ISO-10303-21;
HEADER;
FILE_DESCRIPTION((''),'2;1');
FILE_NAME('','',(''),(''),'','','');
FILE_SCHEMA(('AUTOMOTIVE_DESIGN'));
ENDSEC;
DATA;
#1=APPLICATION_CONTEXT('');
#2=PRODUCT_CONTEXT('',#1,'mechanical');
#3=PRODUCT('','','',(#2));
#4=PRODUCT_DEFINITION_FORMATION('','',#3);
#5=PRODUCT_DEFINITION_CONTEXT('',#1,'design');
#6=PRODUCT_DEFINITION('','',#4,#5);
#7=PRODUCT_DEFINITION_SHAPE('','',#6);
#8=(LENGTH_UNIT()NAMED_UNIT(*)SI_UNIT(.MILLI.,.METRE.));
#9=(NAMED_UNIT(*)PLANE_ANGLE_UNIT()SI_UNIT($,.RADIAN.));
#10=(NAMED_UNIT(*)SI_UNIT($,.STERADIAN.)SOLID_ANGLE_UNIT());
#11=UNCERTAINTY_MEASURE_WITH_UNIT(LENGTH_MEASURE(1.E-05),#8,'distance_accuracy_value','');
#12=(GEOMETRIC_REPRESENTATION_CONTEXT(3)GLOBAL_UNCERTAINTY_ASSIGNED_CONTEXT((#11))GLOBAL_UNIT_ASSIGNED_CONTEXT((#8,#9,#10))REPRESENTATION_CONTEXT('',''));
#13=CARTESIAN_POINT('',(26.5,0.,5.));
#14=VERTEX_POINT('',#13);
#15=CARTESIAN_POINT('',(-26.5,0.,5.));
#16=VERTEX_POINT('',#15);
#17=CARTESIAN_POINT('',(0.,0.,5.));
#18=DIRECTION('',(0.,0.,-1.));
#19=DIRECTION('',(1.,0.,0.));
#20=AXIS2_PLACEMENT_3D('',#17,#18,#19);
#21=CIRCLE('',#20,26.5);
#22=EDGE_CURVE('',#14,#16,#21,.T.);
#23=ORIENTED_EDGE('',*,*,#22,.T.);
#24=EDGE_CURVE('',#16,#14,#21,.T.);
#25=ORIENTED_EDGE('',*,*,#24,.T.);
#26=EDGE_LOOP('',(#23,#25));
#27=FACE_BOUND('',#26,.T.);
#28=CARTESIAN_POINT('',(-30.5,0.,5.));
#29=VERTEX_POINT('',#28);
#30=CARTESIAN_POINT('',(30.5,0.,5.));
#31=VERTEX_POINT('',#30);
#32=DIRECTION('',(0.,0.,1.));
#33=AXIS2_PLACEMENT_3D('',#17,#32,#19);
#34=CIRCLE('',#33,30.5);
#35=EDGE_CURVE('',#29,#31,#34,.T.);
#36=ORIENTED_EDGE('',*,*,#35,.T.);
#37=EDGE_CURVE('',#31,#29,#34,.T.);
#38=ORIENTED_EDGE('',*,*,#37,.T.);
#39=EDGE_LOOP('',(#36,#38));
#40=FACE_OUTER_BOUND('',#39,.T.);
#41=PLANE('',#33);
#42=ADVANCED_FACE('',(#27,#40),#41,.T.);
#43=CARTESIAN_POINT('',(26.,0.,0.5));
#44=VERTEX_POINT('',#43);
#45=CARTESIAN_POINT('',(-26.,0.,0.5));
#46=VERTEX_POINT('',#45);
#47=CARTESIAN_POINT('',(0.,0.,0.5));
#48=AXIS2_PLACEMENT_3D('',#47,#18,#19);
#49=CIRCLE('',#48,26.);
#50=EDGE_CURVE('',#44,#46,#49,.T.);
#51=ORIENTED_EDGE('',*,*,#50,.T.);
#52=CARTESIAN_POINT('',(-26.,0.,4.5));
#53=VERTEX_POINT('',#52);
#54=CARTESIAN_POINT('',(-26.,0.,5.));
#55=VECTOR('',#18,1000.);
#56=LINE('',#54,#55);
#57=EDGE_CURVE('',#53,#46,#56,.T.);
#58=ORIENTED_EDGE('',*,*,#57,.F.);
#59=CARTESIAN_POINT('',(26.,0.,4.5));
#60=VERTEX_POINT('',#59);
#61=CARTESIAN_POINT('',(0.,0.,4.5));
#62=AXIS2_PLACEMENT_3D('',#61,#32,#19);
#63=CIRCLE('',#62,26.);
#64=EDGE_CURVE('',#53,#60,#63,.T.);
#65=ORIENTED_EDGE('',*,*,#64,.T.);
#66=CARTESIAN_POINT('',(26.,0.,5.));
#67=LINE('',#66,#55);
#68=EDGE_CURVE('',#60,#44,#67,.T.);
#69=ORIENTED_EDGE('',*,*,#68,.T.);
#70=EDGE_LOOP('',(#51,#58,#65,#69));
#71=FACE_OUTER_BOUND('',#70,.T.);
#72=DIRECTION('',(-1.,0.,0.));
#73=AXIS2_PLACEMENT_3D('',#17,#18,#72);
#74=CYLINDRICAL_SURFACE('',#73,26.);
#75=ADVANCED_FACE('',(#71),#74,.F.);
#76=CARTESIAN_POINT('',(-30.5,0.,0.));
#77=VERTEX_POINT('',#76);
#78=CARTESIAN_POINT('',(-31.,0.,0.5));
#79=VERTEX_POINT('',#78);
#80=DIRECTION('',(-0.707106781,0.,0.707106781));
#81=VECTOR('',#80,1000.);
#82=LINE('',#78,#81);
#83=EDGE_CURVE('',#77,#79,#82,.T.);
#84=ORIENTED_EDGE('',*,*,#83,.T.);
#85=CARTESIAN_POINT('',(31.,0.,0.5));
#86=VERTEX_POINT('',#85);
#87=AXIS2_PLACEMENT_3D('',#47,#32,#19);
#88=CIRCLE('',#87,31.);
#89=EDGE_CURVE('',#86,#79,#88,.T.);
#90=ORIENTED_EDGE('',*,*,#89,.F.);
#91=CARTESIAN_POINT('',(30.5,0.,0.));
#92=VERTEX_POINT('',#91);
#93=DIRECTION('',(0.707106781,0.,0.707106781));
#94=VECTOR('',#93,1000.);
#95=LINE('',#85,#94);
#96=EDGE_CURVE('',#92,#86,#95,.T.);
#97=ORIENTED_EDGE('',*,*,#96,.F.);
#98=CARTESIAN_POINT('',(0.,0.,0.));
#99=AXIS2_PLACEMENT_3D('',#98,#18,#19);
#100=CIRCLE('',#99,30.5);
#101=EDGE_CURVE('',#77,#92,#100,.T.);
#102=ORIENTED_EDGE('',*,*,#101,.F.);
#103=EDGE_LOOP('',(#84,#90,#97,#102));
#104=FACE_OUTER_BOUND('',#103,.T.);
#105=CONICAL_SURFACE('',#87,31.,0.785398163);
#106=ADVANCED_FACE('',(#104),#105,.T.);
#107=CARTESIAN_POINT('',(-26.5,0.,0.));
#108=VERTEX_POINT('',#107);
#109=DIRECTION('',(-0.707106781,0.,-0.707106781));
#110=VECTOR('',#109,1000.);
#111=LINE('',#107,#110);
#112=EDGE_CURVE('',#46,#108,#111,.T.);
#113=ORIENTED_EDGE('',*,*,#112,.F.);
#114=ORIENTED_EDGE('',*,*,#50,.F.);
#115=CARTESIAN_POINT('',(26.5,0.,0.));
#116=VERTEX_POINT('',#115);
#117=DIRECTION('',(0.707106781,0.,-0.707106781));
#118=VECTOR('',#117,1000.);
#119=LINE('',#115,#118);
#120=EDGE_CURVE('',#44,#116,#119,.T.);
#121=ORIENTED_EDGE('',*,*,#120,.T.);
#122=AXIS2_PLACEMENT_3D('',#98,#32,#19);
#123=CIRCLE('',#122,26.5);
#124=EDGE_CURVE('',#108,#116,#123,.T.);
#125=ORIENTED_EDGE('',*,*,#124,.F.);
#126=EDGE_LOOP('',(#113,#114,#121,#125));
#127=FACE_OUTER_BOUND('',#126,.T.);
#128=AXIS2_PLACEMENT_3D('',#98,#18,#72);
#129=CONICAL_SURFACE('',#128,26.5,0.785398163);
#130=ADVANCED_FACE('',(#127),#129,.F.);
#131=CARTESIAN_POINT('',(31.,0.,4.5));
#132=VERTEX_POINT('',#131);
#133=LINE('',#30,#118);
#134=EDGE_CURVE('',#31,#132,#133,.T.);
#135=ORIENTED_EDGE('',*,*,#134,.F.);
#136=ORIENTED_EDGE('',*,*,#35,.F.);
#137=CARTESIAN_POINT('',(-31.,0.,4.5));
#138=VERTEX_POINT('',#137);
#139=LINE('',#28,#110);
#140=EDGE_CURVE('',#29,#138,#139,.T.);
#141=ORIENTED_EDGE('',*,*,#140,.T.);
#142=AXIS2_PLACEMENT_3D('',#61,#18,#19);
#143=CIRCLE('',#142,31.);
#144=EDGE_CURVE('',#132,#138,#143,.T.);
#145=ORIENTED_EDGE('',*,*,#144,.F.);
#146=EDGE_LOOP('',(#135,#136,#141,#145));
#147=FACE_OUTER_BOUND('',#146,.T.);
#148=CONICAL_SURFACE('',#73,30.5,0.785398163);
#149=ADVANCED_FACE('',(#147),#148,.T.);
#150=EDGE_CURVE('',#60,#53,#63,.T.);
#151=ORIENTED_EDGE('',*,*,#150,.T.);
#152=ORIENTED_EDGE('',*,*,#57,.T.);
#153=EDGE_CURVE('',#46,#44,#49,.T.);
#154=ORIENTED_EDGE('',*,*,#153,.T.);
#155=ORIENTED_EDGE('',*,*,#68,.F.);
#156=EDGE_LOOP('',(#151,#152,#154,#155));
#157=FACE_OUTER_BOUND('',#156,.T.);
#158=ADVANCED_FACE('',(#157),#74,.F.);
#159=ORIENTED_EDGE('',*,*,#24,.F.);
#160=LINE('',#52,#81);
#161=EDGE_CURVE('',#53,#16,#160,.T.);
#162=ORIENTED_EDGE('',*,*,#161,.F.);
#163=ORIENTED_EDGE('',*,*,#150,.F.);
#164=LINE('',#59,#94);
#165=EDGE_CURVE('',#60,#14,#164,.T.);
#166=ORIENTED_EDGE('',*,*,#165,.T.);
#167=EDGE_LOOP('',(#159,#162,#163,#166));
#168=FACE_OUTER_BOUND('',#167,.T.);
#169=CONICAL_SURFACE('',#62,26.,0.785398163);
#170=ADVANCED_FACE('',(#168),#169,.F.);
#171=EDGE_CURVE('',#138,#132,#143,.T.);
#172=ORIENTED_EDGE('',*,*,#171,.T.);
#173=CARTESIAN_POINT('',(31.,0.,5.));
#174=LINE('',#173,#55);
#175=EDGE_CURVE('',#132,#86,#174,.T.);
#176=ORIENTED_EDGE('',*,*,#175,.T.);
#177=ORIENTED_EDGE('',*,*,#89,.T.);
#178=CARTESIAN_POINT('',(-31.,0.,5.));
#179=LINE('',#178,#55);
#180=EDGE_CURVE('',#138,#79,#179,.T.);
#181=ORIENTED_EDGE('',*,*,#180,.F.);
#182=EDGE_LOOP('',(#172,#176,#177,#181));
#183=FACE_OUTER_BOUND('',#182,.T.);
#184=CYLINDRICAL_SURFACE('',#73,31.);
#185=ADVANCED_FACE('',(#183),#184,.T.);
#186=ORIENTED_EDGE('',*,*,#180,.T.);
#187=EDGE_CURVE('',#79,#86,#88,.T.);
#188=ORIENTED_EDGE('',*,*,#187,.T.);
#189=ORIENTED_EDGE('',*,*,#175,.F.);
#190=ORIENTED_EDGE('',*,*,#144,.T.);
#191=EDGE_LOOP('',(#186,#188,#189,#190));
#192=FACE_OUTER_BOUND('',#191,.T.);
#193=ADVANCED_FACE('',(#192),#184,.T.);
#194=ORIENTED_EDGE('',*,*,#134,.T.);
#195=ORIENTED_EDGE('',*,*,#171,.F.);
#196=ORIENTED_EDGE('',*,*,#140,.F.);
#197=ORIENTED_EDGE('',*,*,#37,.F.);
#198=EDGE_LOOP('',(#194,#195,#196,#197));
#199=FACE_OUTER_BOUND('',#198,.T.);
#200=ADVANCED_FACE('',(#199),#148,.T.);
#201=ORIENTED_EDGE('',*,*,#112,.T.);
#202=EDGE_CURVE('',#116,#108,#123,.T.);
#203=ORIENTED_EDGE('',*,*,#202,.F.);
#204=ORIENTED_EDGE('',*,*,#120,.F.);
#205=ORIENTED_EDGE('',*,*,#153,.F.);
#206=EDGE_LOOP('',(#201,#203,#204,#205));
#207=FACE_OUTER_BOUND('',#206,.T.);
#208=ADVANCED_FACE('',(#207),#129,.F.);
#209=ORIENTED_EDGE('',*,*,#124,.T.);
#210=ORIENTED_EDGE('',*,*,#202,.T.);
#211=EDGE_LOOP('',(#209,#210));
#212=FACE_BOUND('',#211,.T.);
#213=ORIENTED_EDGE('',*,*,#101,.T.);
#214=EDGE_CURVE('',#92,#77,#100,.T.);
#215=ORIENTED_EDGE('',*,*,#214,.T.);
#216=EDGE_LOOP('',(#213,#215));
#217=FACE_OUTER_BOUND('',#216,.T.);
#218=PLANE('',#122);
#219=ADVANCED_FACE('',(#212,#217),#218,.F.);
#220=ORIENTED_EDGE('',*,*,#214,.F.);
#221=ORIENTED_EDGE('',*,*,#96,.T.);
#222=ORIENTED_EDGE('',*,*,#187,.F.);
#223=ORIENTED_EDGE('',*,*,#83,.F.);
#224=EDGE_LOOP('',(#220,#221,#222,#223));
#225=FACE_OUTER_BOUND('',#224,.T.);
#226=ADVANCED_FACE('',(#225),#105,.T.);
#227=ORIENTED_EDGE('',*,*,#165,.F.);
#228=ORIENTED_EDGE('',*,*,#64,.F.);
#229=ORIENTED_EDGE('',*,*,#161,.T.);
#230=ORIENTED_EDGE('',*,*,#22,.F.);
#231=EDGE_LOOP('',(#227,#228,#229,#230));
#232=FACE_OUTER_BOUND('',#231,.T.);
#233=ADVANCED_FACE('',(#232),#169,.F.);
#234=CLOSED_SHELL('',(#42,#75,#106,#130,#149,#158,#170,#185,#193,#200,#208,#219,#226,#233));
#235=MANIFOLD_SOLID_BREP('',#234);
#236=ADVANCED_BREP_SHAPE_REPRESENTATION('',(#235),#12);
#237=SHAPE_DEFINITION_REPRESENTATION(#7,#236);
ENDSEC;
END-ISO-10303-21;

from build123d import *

# Parameters (mm, degrees)
SKETCH1_R           = 31
SKETCH1_R_2         = 26
BOSS_EXTRUDE1_DEPTH = 5
CHAMFER1_SIZE       = 0.5


with BuildPart() as part:
    # Sketch1 → Boss-Extrude1 (new body)
    with BuildSketch(Plane.XY):
        Circle(SKETCH1_R)
        Circle(SKETCH1_R_2, mode=Mode.SUBTRACT)
    extrude(amount=BOSS_EXTRUDE1_DEPTH)

    # Chamfer1
    chamfer1_edges = [part.edges().sort_by_distance(p)[0] for p in [
        (-31, 0, 0),
        (-31, 0, 5),
        (-26, 0, 0),
        (-26, 0, 5),
    ]]
    chamfer(chamfer1_edges, length=CHAMFER1_SIZE)


solid = part.part
